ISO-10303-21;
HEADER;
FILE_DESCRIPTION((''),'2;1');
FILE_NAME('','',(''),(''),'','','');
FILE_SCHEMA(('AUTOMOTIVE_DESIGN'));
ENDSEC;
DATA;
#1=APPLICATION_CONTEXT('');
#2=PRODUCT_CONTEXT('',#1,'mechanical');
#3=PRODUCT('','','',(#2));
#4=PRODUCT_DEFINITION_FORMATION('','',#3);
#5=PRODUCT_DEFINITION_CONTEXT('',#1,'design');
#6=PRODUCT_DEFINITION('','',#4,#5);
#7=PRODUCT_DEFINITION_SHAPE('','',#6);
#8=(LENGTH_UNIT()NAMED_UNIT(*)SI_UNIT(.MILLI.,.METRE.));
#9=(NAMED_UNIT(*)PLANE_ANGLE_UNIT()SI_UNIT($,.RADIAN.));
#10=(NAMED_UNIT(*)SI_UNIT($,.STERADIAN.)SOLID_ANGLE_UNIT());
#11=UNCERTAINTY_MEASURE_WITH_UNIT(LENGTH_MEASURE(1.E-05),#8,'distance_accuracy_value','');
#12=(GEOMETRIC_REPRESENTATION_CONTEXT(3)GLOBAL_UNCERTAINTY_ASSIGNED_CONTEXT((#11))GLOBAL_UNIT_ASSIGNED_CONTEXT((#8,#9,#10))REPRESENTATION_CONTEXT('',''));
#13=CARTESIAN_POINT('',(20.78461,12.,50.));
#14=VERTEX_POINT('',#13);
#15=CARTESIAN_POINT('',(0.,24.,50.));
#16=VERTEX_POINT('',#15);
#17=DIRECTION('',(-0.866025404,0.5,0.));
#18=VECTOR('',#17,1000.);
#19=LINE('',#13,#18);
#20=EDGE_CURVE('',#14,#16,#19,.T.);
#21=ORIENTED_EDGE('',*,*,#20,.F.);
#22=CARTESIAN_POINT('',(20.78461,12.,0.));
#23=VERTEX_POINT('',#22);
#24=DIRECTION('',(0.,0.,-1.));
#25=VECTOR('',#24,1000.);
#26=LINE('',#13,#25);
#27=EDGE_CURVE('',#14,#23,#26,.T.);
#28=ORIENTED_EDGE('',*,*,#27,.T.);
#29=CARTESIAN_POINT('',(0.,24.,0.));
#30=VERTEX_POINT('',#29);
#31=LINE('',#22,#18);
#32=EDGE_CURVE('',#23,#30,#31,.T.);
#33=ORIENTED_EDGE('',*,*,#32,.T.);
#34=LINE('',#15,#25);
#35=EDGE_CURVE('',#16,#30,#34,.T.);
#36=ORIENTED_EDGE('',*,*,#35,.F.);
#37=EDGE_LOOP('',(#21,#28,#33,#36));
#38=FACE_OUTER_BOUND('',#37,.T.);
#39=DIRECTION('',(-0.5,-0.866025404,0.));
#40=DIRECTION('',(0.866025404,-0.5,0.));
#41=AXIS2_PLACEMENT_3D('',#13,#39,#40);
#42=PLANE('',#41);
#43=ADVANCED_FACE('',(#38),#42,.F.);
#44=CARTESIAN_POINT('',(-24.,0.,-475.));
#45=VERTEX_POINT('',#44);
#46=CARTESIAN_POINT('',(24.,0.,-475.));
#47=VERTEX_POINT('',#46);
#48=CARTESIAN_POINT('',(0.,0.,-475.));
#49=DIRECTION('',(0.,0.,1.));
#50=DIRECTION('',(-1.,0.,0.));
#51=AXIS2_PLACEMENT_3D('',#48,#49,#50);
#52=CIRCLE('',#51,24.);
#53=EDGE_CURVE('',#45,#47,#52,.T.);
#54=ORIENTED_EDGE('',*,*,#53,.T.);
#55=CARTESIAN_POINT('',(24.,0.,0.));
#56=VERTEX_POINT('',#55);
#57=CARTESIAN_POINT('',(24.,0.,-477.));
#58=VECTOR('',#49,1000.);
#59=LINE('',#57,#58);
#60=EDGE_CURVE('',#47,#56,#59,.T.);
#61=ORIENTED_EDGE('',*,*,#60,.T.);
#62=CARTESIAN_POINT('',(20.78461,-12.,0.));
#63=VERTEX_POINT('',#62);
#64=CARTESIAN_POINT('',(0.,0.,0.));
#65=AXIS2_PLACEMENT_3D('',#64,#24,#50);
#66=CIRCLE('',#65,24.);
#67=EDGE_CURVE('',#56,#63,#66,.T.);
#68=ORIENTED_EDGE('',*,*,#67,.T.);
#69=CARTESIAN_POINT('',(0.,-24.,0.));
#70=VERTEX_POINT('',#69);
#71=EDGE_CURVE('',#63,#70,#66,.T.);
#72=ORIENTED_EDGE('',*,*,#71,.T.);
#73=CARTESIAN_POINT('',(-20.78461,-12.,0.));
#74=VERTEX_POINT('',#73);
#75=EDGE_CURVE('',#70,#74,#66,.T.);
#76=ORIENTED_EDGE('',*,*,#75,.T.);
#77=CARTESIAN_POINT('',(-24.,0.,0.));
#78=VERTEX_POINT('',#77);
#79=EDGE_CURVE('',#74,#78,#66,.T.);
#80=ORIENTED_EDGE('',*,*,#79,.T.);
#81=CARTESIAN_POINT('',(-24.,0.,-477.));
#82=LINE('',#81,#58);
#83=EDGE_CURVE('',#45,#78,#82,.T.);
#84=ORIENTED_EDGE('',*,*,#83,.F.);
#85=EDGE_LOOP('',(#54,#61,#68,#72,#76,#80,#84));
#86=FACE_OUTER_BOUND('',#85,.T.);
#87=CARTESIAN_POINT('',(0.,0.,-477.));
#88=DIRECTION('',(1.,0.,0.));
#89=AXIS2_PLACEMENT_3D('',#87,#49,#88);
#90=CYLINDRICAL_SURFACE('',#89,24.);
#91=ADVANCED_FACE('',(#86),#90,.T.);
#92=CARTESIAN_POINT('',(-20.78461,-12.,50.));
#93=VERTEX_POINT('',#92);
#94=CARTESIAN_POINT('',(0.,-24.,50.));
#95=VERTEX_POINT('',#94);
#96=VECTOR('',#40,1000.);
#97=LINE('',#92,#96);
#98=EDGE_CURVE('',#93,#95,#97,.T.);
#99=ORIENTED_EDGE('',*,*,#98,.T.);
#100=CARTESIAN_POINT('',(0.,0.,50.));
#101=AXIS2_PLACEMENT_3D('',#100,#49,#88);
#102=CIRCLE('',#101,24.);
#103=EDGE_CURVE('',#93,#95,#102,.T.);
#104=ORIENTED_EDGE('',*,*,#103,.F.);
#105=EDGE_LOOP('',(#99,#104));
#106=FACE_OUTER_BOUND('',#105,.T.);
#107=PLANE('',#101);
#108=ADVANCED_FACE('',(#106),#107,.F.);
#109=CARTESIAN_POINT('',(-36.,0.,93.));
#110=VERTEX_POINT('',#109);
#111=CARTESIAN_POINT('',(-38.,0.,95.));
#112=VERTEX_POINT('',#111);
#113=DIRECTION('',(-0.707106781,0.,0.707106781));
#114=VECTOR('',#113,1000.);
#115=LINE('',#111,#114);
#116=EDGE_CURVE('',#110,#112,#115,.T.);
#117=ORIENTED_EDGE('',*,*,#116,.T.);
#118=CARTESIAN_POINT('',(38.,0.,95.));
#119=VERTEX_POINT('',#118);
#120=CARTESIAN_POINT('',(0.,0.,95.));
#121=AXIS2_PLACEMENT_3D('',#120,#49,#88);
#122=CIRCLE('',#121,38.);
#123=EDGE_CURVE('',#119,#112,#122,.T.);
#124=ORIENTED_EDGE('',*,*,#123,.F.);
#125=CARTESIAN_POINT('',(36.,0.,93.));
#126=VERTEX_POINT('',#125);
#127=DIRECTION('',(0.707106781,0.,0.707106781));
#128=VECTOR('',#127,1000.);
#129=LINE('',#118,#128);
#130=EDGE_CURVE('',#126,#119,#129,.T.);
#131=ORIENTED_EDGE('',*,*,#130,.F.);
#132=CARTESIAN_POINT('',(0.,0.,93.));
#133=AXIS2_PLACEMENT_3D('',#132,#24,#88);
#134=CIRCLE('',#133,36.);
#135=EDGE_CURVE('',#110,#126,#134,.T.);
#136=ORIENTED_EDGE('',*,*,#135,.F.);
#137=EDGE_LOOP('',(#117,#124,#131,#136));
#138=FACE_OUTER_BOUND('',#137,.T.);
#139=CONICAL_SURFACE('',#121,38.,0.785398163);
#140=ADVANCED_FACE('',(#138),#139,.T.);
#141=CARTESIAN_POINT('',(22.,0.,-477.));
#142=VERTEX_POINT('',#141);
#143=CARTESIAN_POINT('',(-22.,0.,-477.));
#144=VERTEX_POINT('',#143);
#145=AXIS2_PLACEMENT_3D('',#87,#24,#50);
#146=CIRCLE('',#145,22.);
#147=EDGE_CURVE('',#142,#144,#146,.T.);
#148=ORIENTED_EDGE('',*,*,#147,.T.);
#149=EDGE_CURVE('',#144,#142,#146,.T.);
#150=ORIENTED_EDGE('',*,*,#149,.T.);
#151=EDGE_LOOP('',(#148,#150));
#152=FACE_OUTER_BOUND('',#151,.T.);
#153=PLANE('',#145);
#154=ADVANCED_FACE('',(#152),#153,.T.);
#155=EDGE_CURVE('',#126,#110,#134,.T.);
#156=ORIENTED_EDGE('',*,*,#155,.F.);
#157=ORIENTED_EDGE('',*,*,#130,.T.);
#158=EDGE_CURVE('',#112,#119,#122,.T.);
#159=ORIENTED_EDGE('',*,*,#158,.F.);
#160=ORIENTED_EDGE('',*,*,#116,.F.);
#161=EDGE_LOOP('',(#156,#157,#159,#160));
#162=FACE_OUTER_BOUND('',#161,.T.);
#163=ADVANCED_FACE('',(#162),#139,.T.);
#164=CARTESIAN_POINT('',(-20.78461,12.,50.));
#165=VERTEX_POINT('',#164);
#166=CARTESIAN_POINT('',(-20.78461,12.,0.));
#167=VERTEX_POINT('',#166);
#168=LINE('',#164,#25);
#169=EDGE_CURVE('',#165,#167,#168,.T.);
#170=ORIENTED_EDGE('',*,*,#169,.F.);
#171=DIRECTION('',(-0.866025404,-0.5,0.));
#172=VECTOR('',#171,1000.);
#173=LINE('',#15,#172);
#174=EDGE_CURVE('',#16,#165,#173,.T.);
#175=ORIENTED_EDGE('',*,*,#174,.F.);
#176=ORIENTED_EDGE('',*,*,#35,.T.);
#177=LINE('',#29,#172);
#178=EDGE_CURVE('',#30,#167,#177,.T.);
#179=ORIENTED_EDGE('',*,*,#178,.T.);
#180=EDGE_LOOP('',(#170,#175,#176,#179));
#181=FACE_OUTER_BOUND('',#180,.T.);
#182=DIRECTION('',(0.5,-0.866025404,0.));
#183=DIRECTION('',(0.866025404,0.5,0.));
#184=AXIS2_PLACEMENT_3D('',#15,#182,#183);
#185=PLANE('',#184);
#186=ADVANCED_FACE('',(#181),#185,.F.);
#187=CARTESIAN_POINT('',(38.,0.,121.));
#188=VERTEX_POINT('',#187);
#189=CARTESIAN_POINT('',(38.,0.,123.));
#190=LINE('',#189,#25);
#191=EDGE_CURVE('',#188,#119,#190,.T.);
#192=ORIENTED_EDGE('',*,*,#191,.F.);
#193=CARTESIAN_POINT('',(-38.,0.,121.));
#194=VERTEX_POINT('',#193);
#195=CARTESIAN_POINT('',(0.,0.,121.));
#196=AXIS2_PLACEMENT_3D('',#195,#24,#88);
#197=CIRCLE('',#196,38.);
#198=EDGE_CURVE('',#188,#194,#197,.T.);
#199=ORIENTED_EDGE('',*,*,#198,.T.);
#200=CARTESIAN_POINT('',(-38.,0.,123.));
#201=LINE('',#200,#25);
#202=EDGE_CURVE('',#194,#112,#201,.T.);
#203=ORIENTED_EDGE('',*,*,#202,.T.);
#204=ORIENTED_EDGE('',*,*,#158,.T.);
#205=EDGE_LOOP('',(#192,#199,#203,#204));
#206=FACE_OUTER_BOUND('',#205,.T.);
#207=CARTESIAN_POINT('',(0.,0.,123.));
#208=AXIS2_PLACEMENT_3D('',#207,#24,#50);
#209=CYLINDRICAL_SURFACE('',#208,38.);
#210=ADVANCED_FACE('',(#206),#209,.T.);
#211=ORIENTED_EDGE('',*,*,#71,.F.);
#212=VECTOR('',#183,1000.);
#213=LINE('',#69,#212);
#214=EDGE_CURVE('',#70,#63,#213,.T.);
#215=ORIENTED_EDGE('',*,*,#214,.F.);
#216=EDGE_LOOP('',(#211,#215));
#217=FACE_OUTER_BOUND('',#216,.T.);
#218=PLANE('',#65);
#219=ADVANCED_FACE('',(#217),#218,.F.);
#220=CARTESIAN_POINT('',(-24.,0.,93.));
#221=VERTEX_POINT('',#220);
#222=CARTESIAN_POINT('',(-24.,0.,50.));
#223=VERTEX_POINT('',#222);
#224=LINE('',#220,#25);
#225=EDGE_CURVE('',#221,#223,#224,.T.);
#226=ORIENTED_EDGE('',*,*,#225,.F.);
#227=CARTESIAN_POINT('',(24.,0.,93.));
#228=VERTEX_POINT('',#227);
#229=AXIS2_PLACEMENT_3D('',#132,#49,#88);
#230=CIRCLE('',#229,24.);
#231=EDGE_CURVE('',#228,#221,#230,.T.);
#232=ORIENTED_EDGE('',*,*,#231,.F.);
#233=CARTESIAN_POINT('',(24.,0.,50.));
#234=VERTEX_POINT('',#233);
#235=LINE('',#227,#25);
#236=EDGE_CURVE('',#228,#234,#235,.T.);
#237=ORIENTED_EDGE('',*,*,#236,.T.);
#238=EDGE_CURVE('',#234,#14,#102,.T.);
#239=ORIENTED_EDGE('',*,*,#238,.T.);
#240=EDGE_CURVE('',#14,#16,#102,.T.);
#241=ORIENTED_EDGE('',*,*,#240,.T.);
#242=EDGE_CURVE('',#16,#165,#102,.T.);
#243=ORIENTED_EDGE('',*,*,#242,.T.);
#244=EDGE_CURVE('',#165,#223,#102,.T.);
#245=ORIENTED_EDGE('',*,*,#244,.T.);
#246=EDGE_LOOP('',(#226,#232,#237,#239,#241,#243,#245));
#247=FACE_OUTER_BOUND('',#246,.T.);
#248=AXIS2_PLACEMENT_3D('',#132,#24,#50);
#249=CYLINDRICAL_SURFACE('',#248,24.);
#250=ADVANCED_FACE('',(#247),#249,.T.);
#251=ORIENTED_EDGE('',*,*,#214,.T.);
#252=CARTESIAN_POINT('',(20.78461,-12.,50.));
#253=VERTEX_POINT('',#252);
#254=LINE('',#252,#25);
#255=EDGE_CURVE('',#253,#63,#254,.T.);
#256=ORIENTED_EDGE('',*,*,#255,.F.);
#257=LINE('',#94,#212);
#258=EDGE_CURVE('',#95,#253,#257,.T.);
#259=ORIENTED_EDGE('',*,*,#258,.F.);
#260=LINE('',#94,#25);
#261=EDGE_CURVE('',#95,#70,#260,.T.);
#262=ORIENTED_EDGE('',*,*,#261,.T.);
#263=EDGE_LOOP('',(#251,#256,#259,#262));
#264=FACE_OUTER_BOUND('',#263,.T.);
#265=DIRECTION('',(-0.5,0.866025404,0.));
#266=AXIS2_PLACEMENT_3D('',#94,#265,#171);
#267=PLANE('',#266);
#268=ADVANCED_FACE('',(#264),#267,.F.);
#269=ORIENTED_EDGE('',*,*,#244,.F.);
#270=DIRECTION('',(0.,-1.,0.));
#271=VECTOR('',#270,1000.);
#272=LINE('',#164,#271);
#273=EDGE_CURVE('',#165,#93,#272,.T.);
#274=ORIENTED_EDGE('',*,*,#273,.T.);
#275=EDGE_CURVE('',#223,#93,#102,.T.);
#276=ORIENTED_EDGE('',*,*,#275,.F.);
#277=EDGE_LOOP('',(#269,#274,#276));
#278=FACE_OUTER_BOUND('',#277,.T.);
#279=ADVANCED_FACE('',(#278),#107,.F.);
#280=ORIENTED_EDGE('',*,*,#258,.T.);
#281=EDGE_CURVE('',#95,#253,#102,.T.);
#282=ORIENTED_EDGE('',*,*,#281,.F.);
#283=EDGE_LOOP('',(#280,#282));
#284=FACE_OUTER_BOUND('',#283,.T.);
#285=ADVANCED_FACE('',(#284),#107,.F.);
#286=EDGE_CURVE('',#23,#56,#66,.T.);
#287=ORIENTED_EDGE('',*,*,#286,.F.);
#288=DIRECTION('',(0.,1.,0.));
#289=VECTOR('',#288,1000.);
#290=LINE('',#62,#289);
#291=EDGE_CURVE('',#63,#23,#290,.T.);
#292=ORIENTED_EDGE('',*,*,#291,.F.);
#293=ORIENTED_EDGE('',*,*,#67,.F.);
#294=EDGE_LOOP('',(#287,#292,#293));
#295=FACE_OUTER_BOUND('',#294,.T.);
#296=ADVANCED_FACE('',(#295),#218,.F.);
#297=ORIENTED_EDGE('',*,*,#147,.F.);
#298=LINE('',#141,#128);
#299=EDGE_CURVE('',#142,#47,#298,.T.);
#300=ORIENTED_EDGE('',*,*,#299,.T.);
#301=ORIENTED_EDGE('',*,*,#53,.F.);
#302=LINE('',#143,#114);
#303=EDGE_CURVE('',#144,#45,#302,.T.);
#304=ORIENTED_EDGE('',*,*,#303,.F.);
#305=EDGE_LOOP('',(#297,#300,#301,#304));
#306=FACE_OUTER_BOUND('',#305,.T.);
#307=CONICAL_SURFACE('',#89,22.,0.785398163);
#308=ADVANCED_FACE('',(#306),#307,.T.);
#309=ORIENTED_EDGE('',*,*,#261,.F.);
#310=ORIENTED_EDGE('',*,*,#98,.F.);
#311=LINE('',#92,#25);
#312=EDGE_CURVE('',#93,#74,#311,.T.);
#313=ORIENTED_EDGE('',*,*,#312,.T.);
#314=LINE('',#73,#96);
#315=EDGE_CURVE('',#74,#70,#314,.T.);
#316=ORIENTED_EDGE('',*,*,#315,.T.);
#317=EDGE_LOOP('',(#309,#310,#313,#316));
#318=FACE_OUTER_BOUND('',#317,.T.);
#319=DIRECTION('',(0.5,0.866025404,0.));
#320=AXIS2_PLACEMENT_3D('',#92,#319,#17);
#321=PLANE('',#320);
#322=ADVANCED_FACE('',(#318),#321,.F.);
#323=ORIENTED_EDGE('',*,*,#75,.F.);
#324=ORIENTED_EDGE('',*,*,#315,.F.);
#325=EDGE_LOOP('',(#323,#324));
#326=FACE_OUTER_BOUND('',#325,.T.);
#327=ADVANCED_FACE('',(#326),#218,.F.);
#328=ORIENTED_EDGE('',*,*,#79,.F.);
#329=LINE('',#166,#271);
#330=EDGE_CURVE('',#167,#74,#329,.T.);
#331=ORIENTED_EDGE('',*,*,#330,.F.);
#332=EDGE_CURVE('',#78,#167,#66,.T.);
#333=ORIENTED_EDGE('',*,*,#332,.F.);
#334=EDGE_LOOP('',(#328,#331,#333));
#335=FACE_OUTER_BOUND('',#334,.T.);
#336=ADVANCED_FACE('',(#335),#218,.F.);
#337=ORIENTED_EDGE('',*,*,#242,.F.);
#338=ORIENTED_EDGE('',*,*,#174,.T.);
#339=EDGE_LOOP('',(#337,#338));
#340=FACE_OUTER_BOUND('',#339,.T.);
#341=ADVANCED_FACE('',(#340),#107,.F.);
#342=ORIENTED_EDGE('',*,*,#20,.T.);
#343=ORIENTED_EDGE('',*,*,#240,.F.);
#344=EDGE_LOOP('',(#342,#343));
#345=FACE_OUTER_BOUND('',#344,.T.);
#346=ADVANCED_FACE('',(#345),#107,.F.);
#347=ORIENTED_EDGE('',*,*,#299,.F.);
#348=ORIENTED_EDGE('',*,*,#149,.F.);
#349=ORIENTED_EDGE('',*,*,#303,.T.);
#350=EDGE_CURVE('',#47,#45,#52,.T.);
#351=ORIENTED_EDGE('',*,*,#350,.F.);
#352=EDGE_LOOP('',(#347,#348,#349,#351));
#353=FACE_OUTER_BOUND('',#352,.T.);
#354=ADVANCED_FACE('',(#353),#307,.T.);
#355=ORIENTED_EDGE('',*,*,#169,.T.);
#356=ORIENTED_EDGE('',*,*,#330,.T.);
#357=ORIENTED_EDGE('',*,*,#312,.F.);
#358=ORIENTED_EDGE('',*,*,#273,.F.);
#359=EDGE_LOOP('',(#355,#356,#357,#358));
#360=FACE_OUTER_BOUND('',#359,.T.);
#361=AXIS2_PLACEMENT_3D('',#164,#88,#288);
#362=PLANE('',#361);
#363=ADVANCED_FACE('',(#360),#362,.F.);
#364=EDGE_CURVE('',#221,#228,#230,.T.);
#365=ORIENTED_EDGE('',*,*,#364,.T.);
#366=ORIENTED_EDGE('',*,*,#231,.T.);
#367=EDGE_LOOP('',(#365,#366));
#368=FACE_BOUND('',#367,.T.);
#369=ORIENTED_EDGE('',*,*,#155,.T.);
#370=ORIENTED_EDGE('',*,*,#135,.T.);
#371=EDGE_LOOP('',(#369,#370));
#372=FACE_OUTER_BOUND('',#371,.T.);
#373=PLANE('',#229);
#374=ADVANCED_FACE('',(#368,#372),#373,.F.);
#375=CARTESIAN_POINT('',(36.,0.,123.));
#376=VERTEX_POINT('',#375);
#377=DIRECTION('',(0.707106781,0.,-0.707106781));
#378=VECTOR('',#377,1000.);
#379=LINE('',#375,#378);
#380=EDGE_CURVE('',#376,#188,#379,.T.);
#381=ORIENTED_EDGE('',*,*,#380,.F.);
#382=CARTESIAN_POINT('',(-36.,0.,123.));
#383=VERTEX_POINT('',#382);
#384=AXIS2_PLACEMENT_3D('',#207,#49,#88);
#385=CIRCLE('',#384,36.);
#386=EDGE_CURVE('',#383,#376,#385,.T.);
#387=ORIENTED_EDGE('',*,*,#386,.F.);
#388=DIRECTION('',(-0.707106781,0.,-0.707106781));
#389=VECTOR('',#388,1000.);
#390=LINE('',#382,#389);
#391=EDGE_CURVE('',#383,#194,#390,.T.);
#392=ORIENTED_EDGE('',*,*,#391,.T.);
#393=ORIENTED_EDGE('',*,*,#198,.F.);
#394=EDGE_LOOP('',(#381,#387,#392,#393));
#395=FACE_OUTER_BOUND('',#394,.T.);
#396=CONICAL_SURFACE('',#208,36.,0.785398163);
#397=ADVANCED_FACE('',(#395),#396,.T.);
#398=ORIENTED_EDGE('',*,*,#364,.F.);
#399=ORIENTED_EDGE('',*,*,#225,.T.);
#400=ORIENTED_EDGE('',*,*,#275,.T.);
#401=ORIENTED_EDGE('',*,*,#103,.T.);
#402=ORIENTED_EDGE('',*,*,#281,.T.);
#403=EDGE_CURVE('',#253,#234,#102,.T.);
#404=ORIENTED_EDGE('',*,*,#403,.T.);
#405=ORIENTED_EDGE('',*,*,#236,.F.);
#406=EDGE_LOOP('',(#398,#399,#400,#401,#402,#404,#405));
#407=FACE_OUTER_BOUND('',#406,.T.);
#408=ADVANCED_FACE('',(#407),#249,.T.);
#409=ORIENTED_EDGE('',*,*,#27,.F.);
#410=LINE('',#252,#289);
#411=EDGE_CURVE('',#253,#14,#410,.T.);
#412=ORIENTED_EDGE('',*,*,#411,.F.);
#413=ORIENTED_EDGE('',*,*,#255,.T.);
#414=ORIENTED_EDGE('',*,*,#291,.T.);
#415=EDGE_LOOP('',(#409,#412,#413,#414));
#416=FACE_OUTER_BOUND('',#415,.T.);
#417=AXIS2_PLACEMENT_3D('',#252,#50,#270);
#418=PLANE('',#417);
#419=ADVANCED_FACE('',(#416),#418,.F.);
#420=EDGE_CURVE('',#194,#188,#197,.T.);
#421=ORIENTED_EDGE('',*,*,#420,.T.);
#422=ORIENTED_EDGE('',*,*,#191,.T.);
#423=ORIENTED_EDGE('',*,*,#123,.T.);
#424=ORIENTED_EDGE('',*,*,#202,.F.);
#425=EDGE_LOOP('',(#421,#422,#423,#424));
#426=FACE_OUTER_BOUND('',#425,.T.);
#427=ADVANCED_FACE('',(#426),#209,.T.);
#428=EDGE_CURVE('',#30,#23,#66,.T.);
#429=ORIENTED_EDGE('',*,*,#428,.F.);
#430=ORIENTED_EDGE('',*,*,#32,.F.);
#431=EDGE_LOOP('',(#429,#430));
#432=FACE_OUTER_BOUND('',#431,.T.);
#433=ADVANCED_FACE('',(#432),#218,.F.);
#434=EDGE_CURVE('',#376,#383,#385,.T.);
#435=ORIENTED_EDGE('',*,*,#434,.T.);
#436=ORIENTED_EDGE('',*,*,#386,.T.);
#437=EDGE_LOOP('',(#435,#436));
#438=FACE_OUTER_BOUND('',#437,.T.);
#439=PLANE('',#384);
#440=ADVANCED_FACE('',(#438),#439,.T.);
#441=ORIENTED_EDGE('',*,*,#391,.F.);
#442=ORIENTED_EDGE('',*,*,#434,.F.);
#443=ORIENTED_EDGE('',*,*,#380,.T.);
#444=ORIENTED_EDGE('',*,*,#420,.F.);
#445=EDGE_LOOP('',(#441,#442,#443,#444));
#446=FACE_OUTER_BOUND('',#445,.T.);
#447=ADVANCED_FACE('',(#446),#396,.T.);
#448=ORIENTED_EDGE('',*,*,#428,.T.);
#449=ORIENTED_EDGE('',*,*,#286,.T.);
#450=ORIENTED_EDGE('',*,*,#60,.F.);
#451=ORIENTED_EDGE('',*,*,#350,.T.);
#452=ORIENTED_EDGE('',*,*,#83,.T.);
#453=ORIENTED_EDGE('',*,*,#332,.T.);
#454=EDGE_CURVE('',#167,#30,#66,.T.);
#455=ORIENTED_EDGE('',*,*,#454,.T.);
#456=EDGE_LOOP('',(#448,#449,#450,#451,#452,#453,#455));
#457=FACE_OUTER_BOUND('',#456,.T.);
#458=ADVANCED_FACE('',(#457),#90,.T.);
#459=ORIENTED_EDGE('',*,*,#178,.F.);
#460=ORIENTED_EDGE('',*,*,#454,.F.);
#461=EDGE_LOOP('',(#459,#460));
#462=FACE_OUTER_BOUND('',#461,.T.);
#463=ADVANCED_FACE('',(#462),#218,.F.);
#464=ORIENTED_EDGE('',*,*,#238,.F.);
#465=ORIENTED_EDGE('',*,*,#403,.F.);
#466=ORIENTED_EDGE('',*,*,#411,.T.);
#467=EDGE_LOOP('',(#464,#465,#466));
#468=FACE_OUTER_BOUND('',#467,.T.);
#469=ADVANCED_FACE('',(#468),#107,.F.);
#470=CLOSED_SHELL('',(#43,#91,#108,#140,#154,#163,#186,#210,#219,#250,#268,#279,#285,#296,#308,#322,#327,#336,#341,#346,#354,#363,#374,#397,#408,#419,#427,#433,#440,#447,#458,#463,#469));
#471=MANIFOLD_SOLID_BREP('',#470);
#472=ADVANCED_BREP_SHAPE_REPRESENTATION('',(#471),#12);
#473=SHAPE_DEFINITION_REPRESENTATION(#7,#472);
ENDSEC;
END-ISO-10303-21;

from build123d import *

# Parameters (mm, degrees)
BOSS_EXTRUDE1_DEPTH = 50
SKETCH2_R           = 24
BOSS_EXTRUDE2_DEPTH = 43
SKETCH3_R           = 38
BOSS_EXTRUDE3_DEPTH = 30
BOSS_EXTRUDE4_START = 477
SKETCH4_R           = 24
BOSS_EXTRUDE4_DEPTH = 477
CHAMFER1_SIZE       = 2


with BuildPart() as part:
    # Sketch1 → Boss-Extrude1 (new body)
    with BuildSketch(Plane.XY):
        Polygon((20.784609691, 12), (0, 24), (-20.784609691, 12), (-20.784609691, -12), (0, -24), (20.784609691, -12), align=None)
    extrude(amount=BOSS_EXTRUDE1_DEPTH)

    # Sketch2 → Boss-Extrude2 (add)
    with BuildSketch(Plane.XY.offset(50)):
        with Locations(Location((0, 0, 0), (0, 0, 150))):
            Circle(SKETCH2_R)
    extrude(amount=BOSS_EXTRUDE2_DEPTH)

    # Sketch3 → Boss-Extrude3 (add)
    with BuildSketch(Plane.XY.offset(93)):
        Circle(SKETCH3_R)
    extrude(amount=BOSS_EXTRUDE3_DEPTH)

    # Sketch4 → Boss-Extrude4 (add)
    with BuildSketch(Plane(origin=(0, 0, 0), x_dir=(-1, 0, 0), z_dir=(0, 0, -1)).offset(BOSS_EXTRUDE4_START)):
        with Locations(Location((0, 0, 0), (0, 0, 30))):
            Circle(SKETCH4_R)
    extrude(amount=-BOSS_EXTRUDE4_DEPTH)

    # Chamfer1
    chamfer1_edges = [part.edges().sort_by_distance(p)[0] for p in [
        (-38, 0, 93),
        (-38, 0, 123),
        (20.784609691, -12, -477),
    ]]
    chamfer(chamfer1_edges, length=CHAMFER1_SIZE)


solid = part.part
